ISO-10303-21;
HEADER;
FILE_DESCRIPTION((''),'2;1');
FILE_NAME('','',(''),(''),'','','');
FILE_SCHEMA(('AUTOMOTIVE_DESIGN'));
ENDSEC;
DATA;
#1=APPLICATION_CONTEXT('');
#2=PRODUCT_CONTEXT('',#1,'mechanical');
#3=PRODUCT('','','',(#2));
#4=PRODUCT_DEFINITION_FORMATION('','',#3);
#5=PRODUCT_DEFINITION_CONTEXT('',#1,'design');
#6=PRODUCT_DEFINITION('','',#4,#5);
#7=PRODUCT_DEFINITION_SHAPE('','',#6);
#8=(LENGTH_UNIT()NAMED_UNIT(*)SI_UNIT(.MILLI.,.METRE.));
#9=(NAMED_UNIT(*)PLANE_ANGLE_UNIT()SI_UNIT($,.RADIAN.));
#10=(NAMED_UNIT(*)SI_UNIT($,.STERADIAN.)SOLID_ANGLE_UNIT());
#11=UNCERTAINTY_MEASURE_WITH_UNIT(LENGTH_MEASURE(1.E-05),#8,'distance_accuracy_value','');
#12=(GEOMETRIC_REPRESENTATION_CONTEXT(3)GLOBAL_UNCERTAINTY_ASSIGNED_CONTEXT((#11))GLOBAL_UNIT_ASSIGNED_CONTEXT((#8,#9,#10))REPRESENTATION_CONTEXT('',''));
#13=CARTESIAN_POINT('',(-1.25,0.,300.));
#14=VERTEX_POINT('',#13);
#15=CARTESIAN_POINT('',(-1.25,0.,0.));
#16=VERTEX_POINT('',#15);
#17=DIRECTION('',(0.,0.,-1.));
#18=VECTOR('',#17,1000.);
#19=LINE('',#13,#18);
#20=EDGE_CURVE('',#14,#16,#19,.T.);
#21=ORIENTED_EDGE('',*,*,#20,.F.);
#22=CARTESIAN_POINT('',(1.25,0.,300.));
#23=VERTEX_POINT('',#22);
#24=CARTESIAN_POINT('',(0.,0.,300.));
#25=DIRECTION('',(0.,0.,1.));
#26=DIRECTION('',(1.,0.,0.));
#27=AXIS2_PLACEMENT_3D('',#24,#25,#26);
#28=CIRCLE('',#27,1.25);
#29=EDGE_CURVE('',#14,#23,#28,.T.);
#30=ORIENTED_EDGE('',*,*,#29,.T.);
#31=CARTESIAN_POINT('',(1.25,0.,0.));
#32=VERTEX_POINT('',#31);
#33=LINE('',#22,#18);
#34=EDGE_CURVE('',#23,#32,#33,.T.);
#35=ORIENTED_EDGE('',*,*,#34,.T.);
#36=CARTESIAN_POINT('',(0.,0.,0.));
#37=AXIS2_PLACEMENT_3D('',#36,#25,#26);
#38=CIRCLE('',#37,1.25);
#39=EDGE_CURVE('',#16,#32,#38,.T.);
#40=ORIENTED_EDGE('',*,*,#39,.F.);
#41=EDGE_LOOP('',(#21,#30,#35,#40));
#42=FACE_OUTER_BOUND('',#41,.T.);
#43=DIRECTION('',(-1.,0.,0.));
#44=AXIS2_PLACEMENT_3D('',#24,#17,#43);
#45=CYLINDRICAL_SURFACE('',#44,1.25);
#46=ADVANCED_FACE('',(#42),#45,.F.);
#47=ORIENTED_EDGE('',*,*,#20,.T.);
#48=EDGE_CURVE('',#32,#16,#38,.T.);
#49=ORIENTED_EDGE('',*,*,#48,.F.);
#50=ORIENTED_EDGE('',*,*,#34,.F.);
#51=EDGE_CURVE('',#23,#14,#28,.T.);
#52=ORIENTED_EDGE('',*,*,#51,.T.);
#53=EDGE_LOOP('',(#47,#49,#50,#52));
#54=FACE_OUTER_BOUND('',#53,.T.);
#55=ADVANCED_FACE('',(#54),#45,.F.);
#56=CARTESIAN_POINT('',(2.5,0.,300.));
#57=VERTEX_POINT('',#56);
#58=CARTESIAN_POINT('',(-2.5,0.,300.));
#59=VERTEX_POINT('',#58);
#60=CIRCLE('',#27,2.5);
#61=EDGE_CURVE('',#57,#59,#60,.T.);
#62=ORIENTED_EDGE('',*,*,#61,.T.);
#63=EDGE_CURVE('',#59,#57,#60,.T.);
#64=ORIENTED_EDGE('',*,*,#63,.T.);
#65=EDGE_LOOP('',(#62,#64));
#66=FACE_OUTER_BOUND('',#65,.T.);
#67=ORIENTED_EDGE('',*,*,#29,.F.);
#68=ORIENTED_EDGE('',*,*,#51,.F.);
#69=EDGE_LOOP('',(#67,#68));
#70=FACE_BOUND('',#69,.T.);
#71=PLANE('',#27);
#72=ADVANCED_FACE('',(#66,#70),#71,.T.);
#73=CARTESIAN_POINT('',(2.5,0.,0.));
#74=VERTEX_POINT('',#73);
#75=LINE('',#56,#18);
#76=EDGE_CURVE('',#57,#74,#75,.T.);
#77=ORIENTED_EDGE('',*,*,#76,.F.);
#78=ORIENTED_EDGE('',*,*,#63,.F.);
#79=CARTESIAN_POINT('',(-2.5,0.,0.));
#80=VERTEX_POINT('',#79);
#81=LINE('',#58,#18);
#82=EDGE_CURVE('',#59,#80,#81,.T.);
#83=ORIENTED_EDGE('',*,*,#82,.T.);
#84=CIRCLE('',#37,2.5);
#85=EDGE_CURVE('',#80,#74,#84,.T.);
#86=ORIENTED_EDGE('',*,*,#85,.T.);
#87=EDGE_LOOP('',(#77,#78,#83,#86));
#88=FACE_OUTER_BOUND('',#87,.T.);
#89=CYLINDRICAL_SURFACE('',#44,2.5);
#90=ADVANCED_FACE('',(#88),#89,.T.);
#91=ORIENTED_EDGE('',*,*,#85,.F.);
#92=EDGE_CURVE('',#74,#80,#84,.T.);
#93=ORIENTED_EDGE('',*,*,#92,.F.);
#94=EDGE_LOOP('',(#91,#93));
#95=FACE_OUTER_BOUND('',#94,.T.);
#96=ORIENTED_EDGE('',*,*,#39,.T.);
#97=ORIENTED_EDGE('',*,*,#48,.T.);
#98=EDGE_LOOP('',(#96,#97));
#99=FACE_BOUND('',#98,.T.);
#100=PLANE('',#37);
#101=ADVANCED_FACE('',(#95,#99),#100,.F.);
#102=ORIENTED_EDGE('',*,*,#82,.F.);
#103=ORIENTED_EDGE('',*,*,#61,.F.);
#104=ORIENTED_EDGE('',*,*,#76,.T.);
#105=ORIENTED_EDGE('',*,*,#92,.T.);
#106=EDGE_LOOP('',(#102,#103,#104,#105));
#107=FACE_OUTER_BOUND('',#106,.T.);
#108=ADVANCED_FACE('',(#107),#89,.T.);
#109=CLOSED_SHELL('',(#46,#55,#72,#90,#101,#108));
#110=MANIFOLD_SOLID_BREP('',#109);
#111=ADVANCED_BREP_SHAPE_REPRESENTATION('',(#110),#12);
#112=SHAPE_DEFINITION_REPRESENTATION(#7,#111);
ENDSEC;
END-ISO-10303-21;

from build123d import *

# Parameters (mm, degrees)
SKETCH2_R           = 2.5
SKETCH2_R_2         = 1.25
BOSS_EXTRUDE1_DEPTH = 300


with BuildPart() as part:
    # Sketch2 → Boss-Extrude1 (new body)
    with BuildSketch(Plane.XY):
        Circle(SKETCH2_R)
        Circle(SKETCH2_R_2, mode=Mode.SUBTRACT)
    extrude(amount=BOSS_EXTRUDE1_DEPTH)


solid = part.part
